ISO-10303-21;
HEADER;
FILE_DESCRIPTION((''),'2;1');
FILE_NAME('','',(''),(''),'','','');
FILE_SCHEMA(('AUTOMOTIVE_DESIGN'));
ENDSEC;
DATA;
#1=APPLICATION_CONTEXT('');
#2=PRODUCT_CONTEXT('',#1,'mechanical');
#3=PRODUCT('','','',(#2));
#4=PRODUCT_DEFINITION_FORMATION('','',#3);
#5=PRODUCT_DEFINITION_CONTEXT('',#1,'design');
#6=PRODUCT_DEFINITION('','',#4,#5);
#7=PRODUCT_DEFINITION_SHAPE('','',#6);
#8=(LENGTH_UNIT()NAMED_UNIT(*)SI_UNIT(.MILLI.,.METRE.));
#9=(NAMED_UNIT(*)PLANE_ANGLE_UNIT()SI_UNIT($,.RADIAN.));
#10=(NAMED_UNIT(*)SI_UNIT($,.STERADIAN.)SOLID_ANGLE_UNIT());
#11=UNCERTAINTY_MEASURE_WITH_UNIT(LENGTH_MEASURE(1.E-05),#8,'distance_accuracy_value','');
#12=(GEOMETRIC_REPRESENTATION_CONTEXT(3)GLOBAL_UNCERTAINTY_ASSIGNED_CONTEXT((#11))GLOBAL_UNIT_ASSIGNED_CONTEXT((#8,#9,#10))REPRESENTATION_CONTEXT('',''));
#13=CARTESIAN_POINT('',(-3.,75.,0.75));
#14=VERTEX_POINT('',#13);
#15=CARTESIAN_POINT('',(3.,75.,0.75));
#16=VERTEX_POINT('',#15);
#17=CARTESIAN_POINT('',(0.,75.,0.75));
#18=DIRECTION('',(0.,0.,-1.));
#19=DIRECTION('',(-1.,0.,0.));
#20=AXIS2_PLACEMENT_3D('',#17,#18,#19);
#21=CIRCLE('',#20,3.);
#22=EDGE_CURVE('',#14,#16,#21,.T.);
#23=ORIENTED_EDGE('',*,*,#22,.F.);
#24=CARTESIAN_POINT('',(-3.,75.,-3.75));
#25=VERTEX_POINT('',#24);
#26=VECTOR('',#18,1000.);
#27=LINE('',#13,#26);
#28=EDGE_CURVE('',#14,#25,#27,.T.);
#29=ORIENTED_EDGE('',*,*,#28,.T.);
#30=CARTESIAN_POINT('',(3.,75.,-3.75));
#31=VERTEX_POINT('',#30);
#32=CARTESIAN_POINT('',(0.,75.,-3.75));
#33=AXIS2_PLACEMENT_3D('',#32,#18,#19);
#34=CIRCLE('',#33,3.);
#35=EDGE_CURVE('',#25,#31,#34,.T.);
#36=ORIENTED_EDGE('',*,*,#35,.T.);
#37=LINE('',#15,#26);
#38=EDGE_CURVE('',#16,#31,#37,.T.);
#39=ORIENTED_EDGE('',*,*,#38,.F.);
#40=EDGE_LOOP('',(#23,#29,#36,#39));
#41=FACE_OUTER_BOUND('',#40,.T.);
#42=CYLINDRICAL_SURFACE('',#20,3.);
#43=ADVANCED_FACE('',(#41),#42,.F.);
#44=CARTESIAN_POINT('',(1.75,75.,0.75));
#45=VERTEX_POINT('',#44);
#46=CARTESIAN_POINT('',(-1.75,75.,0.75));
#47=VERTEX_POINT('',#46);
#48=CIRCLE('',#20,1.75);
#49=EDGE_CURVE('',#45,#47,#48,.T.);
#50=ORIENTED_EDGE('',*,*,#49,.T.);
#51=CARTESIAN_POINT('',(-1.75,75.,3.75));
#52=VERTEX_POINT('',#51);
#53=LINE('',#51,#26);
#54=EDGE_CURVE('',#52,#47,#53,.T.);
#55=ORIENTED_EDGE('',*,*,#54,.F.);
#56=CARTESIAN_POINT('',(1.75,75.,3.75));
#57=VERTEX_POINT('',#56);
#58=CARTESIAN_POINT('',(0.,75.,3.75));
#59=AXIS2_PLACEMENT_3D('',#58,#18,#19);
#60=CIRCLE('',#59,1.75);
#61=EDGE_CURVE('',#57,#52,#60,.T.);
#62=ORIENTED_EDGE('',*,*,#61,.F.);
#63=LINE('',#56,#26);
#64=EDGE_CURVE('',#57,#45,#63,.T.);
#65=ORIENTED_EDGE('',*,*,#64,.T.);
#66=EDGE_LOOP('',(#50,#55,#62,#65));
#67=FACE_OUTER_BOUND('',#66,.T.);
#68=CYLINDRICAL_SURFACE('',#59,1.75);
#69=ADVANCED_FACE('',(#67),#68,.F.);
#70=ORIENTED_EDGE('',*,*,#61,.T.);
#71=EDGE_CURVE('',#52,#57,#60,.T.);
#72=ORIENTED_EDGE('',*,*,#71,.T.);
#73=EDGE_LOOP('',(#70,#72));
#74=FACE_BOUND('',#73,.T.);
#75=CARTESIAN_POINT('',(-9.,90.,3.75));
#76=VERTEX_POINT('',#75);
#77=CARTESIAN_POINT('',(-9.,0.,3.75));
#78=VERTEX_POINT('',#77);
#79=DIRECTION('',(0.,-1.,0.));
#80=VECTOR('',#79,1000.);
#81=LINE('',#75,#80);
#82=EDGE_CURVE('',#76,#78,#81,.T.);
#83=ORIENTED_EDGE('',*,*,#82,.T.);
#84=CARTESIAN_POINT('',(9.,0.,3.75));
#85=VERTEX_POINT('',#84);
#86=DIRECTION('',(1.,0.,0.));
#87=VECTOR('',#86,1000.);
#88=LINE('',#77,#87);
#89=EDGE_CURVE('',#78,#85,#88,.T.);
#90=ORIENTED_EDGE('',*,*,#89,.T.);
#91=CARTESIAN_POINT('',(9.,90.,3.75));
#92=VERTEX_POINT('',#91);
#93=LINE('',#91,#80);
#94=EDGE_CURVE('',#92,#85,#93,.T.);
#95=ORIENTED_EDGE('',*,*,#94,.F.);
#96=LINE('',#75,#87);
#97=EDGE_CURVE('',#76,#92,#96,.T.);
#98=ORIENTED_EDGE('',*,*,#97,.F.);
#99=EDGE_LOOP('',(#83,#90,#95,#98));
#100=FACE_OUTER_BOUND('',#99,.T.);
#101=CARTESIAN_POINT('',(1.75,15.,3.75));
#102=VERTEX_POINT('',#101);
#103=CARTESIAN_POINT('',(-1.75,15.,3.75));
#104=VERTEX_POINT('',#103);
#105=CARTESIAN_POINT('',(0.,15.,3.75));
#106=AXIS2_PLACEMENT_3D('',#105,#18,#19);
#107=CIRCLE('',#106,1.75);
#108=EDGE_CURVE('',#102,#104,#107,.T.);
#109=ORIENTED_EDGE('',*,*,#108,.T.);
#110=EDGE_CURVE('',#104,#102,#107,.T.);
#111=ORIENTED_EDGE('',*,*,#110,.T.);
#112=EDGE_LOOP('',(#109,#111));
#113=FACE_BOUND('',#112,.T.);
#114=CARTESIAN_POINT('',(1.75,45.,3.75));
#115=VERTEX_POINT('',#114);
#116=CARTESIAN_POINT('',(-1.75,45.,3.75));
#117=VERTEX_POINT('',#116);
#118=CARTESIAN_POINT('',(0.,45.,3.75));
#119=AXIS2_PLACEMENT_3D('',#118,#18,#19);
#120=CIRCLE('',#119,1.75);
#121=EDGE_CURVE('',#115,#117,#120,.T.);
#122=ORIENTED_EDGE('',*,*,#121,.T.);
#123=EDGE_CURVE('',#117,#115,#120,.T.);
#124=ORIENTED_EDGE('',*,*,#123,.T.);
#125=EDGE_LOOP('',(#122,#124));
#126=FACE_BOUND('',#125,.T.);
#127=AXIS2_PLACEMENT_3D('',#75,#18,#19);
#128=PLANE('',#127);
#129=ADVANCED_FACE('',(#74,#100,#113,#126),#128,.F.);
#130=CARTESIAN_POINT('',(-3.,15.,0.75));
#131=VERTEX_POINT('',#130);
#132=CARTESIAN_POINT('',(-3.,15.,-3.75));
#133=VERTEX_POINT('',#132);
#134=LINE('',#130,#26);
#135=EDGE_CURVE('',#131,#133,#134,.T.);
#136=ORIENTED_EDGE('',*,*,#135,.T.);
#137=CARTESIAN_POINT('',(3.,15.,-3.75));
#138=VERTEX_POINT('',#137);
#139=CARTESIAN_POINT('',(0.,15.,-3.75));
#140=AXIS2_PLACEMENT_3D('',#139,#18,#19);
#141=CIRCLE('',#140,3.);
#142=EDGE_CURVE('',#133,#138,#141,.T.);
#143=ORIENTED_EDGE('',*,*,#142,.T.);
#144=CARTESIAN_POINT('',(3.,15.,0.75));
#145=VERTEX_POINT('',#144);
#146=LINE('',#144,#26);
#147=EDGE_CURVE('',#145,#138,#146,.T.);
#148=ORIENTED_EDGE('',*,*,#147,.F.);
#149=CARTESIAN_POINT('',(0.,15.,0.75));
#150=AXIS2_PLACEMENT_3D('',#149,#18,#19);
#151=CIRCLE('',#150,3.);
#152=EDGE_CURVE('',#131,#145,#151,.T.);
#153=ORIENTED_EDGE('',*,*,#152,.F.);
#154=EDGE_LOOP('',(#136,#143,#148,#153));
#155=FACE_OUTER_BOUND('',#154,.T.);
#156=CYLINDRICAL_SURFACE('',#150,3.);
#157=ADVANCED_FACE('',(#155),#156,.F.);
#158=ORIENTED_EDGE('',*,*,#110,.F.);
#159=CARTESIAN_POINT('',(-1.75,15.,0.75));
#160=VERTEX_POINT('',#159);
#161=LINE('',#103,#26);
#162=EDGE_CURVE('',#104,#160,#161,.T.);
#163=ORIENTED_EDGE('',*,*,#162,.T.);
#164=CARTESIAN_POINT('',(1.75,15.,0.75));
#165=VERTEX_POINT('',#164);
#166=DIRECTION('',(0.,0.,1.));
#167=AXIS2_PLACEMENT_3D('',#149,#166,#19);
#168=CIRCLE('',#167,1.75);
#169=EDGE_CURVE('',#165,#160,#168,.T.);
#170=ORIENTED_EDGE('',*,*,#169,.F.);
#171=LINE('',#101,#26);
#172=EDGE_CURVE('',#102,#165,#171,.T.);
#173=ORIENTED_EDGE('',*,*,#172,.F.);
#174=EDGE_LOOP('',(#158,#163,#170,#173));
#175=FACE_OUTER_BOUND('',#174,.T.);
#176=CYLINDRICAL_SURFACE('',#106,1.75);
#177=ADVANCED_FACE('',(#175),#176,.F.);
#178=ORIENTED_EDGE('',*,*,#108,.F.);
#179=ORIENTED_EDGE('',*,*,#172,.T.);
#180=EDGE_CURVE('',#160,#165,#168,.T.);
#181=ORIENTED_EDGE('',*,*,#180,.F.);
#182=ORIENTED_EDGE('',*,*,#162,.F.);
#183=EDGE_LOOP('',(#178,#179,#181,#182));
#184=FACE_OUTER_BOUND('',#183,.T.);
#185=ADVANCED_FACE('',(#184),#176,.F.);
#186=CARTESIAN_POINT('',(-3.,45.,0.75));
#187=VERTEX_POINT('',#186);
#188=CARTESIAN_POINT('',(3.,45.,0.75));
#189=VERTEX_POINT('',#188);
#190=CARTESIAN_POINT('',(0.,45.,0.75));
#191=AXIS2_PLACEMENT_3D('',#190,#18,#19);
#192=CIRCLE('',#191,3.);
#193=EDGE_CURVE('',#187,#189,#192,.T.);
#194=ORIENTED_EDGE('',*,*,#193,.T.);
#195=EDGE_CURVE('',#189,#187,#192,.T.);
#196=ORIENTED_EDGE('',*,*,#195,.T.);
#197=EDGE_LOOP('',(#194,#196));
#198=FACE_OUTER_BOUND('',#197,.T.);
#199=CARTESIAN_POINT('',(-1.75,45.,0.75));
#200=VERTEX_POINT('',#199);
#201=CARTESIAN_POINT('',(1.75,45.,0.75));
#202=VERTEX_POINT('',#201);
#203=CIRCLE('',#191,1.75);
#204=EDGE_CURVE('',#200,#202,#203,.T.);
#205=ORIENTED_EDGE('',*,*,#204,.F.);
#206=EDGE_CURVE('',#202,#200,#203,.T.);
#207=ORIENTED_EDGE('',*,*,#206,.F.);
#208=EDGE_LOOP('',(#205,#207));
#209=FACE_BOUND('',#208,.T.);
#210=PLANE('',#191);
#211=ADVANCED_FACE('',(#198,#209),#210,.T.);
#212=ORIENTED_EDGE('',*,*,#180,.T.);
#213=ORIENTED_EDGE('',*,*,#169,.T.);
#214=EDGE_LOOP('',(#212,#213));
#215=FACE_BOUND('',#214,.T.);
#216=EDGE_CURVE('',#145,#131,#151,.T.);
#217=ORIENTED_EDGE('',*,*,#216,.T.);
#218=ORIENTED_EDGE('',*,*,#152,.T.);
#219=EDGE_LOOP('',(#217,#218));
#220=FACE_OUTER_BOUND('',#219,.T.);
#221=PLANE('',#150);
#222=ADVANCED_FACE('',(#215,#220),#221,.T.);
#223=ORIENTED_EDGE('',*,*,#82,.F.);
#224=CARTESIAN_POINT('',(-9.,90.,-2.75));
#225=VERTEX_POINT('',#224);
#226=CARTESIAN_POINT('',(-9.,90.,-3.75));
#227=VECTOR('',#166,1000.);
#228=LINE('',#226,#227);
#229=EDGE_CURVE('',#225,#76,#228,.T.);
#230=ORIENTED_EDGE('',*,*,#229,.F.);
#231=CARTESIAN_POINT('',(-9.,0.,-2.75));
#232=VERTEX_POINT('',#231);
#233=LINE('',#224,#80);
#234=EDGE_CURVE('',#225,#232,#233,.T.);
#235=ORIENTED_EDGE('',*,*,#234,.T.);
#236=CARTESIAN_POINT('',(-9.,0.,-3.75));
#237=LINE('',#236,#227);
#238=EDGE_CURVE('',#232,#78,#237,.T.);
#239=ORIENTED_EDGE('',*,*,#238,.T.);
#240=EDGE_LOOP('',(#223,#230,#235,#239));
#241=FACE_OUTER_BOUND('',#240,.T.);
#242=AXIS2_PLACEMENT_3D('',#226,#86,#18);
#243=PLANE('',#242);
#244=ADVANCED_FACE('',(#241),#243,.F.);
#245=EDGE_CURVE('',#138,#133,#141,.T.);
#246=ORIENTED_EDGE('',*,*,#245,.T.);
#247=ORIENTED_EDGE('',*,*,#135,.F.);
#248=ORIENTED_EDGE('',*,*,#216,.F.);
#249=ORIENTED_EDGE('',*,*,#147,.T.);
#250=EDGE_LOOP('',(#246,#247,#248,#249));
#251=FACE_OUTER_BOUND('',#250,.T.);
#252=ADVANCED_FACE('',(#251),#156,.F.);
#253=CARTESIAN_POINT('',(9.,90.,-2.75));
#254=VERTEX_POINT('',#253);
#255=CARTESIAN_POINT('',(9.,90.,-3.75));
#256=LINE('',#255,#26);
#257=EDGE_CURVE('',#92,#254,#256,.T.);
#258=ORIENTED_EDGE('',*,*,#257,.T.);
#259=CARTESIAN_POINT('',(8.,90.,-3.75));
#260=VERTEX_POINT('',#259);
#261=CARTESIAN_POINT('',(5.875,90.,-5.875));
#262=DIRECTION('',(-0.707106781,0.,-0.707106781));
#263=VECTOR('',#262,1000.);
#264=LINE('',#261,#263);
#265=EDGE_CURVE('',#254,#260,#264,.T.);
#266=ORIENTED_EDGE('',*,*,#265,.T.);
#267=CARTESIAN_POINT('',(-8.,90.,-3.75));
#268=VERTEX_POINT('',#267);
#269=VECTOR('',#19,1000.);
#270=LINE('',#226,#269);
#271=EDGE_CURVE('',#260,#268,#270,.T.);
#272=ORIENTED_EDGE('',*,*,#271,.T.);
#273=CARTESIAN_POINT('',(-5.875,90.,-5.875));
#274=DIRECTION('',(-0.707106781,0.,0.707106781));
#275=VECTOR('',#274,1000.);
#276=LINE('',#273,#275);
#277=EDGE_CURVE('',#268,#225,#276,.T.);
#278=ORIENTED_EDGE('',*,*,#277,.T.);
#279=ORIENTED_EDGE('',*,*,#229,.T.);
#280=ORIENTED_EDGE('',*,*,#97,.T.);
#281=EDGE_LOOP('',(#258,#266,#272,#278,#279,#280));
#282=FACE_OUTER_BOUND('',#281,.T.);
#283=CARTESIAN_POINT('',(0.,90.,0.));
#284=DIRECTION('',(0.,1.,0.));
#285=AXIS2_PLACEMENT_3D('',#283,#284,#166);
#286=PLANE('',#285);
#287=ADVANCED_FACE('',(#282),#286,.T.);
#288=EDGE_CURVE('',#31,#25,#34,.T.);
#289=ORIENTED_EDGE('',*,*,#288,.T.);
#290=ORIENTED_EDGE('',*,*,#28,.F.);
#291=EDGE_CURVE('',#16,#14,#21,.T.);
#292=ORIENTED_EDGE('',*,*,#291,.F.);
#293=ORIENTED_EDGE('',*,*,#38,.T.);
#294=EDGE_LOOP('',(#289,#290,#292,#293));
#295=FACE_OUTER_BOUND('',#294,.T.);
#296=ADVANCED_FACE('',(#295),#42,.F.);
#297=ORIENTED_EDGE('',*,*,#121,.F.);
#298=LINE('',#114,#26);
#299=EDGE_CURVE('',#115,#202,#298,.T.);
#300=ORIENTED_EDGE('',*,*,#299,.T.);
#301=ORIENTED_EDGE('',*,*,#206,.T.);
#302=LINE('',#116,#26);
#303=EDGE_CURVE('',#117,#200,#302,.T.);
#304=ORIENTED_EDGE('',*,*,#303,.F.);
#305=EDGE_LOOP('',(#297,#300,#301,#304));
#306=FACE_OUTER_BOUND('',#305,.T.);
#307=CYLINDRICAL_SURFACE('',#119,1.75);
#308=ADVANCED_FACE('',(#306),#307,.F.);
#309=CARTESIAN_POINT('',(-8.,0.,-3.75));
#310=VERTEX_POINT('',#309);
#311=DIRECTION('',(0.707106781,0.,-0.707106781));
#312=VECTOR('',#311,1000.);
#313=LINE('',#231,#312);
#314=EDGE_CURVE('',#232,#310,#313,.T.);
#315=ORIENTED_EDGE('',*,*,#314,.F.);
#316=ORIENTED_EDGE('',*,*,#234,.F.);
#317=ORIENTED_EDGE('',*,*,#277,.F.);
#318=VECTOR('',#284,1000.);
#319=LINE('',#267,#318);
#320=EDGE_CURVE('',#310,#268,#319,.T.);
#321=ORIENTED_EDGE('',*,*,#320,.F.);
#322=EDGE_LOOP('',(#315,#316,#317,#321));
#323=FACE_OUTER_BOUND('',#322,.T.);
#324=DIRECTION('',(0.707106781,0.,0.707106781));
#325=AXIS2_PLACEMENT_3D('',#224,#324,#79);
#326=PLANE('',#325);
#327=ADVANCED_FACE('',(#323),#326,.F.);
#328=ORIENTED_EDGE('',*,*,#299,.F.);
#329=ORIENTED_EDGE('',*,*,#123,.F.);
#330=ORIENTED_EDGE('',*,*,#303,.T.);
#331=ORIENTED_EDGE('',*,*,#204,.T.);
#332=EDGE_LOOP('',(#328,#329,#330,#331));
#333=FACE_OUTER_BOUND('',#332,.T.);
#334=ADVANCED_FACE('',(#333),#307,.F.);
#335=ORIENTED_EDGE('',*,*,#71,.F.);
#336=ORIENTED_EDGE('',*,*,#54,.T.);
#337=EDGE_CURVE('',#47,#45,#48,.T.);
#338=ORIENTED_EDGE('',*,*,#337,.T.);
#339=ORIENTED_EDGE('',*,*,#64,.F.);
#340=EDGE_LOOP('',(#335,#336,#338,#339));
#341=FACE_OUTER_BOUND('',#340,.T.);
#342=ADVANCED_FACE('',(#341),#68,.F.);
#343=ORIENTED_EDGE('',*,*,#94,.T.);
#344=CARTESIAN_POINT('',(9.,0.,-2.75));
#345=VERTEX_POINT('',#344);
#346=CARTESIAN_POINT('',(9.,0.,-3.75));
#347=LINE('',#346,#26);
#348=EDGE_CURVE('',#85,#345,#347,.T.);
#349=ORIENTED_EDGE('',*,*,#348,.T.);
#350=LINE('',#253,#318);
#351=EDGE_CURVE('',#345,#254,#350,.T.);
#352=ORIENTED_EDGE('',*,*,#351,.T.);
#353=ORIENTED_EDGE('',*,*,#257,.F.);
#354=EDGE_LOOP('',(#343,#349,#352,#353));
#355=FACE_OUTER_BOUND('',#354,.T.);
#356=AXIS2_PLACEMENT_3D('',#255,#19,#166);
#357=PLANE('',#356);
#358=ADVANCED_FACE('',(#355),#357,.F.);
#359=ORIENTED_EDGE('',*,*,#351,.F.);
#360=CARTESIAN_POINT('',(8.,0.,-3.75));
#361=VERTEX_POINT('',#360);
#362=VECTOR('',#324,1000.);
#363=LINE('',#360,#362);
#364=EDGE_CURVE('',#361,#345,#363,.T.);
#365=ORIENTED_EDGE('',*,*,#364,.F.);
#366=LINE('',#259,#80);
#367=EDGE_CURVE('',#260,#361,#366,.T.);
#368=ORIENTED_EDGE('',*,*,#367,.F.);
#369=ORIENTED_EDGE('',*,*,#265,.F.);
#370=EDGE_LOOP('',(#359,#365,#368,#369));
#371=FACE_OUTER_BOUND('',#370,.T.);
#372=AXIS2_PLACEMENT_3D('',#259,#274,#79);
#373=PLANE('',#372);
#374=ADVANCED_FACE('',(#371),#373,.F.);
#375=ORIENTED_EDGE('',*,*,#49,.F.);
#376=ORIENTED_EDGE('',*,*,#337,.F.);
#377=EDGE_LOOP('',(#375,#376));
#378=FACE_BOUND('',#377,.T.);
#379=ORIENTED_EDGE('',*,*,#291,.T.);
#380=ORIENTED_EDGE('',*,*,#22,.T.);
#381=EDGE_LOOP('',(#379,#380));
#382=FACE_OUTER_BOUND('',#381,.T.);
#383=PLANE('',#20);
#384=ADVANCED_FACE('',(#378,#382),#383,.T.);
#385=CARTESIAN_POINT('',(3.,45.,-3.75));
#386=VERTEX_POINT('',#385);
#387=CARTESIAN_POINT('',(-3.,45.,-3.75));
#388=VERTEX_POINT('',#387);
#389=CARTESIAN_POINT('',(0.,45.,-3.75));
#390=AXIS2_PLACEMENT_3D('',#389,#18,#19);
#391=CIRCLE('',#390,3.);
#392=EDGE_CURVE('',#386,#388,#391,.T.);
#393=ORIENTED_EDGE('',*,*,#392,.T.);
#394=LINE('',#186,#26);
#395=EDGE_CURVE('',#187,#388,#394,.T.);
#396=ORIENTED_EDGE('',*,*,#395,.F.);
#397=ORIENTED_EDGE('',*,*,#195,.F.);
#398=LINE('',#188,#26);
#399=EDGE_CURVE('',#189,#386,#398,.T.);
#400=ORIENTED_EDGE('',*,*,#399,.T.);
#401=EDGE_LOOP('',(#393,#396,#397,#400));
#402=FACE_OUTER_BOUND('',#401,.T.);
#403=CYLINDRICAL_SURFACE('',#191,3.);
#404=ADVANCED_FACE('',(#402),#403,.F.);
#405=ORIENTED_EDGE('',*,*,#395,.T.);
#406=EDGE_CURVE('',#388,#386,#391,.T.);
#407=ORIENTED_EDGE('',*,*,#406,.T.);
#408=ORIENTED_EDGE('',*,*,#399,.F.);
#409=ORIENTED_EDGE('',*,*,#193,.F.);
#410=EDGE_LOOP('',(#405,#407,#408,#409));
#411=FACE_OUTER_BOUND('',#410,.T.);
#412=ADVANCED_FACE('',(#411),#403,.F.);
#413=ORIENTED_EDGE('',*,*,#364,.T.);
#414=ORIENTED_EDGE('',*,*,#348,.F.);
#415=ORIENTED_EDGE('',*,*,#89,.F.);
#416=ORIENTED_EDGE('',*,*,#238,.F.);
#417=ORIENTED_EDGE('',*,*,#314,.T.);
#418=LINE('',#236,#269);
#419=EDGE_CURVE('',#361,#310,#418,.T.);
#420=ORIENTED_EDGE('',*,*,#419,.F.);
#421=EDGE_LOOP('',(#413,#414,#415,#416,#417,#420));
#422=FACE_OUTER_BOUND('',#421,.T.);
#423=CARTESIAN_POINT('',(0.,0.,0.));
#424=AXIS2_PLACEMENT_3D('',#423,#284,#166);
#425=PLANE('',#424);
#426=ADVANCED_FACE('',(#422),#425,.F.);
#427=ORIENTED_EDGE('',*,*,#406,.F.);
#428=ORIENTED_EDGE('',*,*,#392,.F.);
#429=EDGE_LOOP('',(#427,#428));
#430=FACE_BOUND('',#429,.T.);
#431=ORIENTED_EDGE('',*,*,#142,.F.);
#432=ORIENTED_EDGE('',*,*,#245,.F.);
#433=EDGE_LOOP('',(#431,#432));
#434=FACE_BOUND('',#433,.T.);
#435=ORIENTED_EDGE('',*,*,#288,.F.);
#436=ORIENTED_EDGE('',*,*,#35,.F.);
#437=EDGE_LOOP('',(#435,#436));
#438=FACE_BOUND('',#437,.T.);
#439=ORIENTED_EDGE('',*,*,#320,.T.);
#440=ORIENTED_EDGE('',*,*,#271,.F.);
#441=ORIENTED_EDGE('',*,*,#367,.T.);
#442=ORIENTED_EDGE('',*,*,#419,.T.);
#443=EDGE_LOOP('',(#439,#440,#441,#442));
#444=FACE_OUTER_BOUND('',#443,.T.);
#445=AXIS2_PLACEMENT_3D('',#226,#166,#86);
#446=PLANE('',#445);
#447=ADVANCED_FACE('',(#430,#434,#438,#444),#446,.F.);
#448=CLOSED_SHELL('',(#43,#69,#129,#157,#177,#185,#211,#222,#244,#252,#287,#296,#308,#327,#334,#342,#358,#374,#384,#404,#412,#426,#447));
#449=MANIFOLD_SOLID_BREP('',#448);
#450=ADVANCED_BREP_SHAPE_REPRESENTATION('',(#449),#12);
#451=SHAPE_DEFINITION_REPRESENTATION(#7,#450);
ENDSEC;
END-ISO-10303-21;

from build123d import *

# Parameters (mm, degrees)
SKETCH1_W           = 18
SKETCH1_H           = 7.5
BOSS_EXTRUDE1_DEPTH = 90
CHAMFER1_SIZE       = 1
SKETCH2_R           = 1.75
CUT_EXTRUDE1_DEPTH  = 91.759297044
SKETCH3_R           = 3
CUT_EXTRUDE2_DEPTH  = 4.5
LPATTERN1_COUNT     = 4
LPATTERN1_PITCH     = 30
LPATTERN2_COUNT     = 4
LPATTERN2_PITCH     = 30


with BuildPart() as part:
    # Sketch1 → Boss-Extrude1 (new body)
    with BuildSketch(Plane(origin=(0, 0, 0), x_dir=(1, 0, 0), z_dir=(0, 1, 0))):
        Rectangle(SKETCH1_W, SKETCH1_H)
    extrude(amount=BOSS_EXTRUDE1_DEPTH)

    # Chamfer1
    chamfer1_edges = [part.edges().sort_by_distance(p)[0] for p in [
        (-9, 45, -3.75),
        (9, 45, -3.75),
    ]]
    chamfer(chamfer1_edges, length=CHAMFER1_SIZE)

    # Sketch2 → Cut-Extrude1 (cut, through all)
    with BuildSketch(Plane(origin=(0, 0, -3.75), x_dir=(-1, 0, 0), z_dir=(0, 0, -1))):
        with Locations((0, 15)):
            Circle(SKETCH2_R)
    cut_extrude1 = extrude(amount=-CUT_EXTRUDE1_DEPTH, mode=Mode.SUBTRACT)

    # Sketch3 → Cut-Extrude2 (cut)
    with BuildSketch(Plane(origin=(0, 0, -3.75), x_dir=(-1, 0, 0), z_dir=(0, 0, -1))):
        with Locations((0, 15)):
            Circle(SKETCH3_R)
    cut_extrude2 = extrude(amount=-CUT_EXTRUDE2_DEPTH, mode=Mode.SUBTRACT)

    # LPattern1: Cut-Extrude2 ×4
    with Locations(*[(0, i * LPATTERN1_PITCH, 0) for i in range(1, LPATTERN1_COUNT)]):
        add(cut_extrude2, mode=Mode.SUBTRACT)

    # LPattern2: Cut-Extrude1 ×4
    with Locations(*[(0, i * LPATTERN2_PITCH, 0) for i in range(1, LPATTERN2_COUNT)]):
        add(cut_extrude1, mode=Mode.SUBTRACT)


solid = part.part
